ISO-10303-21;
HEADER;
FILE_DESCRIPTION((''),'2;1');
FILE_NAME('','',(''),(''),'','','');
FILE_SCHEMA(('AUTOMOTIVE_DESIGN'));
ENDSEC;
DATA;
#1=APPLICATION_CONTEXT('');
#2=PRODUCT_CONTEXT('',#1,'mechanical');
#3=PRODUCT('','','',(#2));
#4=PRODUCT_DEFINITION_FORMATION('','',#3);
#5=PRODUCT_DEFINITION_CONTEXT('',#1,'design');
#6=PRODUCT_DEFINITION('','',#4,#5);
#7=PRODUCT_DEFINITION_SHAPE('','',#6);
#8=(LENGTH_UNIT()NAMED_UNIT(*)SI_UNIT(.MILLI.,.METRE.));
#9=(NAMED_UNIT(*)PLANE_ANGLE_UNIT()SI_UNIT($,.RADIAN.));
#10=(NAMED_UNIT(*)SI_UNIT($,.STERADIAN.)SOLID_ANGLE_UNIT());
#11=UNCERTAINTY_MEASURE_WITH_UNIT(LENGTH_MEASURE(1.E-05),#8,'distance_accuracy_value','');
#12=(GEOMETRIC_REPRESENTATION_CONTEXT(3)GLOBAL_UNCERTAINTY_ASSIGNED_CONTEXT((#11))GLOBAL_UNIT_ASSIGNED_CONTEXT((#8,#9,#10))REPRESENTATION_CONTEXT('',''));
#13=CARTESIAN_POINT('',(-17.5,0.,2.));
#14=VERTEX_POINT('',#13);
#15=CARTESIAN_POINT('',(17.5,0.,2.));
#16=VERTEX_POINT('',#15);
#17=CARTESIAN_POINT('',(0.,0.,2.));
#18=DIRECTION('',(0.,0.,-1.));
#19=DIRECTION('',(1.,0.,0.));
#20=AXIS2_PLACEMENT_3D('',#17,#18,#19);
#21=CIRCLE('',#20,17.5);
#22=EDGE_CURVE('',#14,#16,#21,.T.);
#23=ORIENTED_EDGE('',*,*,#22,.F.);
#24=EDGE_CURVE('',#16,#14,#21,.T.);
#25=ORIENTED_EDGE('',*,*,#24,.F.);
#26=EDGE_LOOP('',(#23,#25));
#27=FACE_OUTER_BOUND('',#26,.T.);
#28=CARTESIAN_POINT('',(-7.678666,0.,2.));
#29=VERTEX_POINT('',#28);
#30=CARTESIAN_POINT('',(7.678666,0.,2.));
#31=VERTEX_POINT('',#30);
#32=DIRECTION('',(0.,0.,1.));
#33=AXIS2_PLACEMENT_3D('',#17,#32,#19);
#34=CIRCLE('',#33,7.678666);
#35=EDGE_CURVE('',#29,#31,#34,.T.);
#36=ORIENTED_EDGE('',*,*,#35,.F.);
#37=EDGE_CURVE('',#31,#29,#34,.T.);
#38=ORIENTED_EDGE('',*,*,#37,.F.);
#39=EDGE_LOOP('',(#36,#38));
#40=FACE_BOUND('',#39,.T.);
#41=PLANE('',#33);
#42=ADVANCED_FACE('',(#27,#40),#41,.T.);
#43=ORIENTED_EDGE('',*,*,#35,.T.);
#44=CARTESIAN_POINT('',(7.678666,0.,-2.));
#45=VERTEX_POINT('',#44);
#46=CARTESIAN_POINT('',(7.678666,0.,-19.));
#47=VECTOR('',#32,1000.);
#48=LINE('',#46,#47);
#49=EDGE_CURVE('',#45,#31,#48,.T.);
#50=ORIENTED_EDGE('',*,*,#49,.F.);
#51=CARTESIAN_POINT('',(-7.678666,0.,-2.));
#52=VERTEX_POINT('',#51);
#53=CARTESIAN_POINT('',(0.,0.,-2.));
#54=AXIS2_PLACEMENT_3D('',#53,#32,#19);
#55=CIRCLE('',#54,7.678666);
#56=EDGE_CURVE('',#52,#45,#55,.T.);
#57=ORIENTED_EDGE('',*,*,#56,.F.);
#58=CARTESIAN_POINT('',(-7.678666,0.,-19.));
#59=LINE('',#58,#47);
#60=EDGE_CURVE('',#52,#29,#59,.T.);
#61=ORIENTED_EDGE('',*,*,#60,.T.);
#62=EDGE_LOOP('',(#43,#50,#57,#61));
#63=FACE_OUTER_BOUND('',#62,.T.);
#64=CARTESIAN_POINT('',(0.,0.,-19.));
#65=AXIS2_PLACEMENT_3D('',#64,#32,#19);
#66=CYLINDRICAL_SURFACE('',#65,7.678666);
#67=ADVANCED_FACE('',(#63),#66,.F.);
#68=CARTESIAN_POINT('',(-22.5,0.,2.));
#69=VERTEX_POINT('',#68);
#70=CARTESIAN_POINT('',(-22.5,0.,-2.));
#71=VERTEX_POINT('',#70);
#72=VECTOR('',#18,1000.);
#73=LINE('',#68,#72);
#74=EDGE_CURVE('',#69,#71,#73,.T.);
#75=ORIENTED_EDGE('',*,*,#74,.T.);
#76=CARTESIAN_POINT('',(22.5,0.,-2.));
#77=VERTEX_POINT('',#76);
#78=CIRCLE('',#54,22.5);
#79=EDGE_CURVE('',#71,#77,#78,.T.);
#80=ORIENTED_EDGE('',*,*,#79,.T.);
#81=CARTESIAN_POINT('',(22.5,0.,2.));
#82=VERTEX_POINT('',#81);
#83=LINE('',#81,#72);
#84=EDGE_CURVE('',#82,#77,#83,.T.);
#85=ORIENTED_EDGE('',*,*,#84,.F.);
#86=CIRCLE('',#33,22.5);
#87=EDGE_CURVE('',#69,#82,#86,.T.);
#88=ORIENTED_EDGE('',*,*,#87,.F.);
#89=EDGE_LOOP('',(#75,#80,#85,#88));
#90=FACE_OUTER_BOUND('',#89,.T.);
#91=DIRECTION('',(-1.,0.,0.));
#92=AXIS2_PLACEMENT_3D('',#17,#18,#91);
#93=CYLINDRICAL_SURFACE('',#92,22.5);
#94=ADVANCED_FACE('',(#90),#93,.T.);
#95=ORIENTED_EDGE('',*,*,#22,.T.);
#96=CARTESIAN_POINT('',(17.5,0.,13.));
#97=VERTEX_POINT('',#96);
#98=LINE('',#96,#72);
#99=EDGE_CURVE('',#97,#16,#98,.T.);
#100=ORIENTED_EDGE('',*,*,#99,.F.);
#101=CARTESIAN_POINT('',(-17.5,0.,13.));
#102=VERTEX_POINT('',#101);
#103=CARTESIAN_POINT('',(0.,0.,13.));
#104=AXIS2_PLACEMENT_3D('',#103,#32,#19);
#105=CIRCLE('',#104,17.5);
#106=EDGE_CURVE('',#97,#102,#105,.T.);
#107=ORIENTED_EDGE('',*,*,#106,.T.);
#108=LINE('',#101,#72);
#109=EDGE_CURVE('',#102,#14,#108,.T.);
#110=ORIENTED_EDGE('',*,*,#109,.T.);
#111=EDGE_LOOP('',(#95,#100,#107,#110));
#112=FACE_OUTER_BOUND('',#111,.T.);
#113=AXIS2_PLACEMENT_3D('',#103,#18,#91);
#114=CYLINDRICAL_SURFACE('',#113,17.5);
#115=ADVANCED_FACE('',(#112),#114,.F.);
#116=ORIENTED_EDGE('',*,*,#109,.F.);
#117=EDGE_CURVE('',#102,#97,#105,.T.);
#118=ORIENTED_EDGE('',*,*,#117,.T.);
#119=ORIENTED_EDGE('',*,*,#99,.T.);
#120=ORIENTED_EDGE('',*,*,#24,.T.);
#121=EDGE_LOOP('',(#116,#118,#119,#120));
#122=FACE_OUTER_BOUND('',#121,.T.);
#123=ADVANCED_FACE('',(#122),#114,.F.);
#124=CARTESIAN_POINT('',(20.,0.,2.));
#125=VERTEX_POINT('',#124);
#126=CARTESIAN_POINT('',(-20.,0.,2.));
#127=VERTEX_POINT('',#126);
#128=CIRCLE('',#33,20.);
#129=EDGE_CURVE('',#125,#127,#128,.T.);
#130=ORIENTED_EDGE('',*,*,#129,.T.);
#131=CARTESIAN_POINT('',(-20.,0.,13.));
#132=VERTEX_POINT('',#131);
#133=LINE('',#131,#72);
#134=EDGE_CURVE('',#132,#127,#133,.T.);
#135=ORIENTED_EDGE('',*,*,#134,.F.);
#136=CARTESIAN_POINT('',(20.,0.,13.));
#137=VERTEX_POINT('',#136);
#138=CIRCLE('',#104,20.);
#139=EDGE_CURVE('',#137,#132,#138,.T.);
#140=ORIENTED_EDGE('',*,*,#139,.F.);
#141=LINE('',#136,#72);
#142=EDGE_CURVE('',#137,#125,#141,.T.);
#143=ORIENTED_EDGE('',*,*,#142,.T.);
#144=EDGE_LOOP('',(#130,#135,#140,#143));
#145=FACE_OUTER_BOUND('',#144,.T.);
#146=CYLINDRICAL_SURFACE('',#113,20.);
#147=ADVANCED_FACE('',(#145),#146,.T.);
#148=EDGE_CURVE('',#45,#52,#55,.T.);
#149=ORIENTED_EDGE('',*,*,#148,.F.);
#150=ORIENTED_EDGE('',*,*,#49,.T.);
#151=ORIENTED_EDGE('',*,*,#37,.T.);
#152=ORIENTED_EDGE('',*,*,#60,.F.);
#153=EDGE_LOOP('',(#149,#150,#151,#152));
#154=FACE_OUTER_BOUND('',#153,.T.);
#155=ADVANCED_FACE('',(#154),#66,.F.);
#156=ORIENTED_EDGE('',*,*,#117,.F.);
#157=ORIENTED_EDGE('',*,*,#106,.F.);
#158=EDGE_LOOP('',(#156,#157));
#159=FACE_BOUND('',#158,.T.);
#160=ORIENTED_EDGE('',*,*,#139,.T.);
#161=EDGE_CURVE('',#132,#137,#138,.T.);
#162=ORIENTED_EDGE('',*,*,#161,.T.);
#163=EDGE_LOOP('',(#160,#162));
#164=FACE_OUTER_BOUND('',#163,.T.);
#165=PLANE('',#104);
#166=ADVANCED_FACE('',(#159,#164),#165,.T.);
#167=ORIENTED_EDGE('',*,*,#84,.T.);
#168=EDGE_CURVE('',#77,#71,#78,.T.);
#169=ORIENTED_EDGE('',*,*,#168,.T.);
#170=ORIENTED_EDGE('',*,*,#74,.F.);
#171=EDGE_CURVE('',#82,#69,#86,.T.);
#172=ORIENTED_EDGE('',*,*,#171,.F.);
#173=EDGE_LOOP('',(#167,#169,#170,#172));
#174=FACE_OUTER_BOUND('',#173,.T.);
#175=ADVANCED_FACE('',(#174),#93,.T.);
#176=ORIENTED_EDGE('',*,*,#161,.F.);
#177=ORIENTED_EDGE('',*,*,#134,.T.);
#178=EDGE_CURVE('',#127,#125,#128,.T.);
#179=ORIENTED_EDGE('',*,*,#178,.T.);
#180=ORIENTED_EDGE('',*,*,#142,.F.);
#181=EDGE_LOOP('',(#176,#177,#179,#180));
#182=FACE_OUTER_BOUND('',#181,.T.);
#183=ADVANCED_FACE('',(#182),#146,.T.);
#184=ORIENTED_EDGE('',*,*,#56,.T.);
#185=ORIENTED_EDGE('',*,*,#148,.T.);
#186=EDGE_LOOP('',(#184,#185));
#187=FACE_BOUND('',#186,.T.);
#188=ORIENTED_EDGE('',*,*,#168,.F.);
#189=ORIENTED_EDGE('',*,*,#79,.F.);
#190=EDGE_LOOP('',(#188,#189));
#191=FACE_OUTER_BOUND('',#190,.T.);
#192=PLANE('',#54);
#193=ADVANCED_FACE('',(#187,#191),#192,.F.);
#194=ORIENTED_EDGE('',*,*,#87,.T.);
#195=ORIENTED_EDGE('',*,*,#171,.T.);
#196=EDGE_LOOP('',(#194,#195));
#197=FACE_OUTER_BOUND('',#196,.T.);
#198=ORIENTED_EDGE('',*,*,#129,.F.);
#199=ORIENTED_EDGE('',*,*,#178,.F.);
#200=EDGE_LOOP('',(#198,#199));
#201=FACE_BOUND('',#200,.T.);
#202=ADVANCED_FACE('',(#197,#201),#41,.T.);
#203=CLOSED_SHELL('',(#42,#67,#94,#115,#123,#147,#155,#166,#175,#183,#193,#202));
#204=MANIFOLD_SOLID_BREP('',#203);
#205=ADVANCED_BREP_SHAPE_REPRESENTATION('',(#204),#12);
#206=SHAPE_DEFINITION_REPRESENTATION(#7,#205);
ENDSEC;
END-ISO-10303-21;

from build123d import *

# Parameters (mm, degrees)
SKETCH_1_R          = 22.5
EXTRUDE_1_DEPTH     = 2
SKETCH_2_R          = 20
SKETCH_2_R_2        = 17.5
EXTRUDE_2_DEPTH     = 11
SKETCH_3_R          = 7.678665591
CUT_EXTRUDE_1_DEPTH = 21


with BuildPart() as part:
    # 草图1 → 凸台-拉伸1 (new, symmetric)
    with BuildSketch(Plane.XY):
        Circle(SKETCH_1_R)
    extrude(amount=EXTRUDE_1_DEPTH, both=True)

    # 草图2 → 凸台-拉伸2 (add)
    with BuildSketch(Plane.XY.offset(2)):
        Circle(SKETCH_2_R)
        Circle(SKETCH_2_R_2, mode=Mode.SUBTRACT)
    extrude(amount=EXTRUDE_2_DEPTH)

    # 草图3 → 切除-拉伸1 (cut)
    with BuildSketch(Plane.XY.offset(2)):
        Circle(SKETCH_3_R)
    extrude(amount=-CUT_EXTRUDE_1_DEPTH, mode=Mode.SUBTRACT)


solid = part.part
